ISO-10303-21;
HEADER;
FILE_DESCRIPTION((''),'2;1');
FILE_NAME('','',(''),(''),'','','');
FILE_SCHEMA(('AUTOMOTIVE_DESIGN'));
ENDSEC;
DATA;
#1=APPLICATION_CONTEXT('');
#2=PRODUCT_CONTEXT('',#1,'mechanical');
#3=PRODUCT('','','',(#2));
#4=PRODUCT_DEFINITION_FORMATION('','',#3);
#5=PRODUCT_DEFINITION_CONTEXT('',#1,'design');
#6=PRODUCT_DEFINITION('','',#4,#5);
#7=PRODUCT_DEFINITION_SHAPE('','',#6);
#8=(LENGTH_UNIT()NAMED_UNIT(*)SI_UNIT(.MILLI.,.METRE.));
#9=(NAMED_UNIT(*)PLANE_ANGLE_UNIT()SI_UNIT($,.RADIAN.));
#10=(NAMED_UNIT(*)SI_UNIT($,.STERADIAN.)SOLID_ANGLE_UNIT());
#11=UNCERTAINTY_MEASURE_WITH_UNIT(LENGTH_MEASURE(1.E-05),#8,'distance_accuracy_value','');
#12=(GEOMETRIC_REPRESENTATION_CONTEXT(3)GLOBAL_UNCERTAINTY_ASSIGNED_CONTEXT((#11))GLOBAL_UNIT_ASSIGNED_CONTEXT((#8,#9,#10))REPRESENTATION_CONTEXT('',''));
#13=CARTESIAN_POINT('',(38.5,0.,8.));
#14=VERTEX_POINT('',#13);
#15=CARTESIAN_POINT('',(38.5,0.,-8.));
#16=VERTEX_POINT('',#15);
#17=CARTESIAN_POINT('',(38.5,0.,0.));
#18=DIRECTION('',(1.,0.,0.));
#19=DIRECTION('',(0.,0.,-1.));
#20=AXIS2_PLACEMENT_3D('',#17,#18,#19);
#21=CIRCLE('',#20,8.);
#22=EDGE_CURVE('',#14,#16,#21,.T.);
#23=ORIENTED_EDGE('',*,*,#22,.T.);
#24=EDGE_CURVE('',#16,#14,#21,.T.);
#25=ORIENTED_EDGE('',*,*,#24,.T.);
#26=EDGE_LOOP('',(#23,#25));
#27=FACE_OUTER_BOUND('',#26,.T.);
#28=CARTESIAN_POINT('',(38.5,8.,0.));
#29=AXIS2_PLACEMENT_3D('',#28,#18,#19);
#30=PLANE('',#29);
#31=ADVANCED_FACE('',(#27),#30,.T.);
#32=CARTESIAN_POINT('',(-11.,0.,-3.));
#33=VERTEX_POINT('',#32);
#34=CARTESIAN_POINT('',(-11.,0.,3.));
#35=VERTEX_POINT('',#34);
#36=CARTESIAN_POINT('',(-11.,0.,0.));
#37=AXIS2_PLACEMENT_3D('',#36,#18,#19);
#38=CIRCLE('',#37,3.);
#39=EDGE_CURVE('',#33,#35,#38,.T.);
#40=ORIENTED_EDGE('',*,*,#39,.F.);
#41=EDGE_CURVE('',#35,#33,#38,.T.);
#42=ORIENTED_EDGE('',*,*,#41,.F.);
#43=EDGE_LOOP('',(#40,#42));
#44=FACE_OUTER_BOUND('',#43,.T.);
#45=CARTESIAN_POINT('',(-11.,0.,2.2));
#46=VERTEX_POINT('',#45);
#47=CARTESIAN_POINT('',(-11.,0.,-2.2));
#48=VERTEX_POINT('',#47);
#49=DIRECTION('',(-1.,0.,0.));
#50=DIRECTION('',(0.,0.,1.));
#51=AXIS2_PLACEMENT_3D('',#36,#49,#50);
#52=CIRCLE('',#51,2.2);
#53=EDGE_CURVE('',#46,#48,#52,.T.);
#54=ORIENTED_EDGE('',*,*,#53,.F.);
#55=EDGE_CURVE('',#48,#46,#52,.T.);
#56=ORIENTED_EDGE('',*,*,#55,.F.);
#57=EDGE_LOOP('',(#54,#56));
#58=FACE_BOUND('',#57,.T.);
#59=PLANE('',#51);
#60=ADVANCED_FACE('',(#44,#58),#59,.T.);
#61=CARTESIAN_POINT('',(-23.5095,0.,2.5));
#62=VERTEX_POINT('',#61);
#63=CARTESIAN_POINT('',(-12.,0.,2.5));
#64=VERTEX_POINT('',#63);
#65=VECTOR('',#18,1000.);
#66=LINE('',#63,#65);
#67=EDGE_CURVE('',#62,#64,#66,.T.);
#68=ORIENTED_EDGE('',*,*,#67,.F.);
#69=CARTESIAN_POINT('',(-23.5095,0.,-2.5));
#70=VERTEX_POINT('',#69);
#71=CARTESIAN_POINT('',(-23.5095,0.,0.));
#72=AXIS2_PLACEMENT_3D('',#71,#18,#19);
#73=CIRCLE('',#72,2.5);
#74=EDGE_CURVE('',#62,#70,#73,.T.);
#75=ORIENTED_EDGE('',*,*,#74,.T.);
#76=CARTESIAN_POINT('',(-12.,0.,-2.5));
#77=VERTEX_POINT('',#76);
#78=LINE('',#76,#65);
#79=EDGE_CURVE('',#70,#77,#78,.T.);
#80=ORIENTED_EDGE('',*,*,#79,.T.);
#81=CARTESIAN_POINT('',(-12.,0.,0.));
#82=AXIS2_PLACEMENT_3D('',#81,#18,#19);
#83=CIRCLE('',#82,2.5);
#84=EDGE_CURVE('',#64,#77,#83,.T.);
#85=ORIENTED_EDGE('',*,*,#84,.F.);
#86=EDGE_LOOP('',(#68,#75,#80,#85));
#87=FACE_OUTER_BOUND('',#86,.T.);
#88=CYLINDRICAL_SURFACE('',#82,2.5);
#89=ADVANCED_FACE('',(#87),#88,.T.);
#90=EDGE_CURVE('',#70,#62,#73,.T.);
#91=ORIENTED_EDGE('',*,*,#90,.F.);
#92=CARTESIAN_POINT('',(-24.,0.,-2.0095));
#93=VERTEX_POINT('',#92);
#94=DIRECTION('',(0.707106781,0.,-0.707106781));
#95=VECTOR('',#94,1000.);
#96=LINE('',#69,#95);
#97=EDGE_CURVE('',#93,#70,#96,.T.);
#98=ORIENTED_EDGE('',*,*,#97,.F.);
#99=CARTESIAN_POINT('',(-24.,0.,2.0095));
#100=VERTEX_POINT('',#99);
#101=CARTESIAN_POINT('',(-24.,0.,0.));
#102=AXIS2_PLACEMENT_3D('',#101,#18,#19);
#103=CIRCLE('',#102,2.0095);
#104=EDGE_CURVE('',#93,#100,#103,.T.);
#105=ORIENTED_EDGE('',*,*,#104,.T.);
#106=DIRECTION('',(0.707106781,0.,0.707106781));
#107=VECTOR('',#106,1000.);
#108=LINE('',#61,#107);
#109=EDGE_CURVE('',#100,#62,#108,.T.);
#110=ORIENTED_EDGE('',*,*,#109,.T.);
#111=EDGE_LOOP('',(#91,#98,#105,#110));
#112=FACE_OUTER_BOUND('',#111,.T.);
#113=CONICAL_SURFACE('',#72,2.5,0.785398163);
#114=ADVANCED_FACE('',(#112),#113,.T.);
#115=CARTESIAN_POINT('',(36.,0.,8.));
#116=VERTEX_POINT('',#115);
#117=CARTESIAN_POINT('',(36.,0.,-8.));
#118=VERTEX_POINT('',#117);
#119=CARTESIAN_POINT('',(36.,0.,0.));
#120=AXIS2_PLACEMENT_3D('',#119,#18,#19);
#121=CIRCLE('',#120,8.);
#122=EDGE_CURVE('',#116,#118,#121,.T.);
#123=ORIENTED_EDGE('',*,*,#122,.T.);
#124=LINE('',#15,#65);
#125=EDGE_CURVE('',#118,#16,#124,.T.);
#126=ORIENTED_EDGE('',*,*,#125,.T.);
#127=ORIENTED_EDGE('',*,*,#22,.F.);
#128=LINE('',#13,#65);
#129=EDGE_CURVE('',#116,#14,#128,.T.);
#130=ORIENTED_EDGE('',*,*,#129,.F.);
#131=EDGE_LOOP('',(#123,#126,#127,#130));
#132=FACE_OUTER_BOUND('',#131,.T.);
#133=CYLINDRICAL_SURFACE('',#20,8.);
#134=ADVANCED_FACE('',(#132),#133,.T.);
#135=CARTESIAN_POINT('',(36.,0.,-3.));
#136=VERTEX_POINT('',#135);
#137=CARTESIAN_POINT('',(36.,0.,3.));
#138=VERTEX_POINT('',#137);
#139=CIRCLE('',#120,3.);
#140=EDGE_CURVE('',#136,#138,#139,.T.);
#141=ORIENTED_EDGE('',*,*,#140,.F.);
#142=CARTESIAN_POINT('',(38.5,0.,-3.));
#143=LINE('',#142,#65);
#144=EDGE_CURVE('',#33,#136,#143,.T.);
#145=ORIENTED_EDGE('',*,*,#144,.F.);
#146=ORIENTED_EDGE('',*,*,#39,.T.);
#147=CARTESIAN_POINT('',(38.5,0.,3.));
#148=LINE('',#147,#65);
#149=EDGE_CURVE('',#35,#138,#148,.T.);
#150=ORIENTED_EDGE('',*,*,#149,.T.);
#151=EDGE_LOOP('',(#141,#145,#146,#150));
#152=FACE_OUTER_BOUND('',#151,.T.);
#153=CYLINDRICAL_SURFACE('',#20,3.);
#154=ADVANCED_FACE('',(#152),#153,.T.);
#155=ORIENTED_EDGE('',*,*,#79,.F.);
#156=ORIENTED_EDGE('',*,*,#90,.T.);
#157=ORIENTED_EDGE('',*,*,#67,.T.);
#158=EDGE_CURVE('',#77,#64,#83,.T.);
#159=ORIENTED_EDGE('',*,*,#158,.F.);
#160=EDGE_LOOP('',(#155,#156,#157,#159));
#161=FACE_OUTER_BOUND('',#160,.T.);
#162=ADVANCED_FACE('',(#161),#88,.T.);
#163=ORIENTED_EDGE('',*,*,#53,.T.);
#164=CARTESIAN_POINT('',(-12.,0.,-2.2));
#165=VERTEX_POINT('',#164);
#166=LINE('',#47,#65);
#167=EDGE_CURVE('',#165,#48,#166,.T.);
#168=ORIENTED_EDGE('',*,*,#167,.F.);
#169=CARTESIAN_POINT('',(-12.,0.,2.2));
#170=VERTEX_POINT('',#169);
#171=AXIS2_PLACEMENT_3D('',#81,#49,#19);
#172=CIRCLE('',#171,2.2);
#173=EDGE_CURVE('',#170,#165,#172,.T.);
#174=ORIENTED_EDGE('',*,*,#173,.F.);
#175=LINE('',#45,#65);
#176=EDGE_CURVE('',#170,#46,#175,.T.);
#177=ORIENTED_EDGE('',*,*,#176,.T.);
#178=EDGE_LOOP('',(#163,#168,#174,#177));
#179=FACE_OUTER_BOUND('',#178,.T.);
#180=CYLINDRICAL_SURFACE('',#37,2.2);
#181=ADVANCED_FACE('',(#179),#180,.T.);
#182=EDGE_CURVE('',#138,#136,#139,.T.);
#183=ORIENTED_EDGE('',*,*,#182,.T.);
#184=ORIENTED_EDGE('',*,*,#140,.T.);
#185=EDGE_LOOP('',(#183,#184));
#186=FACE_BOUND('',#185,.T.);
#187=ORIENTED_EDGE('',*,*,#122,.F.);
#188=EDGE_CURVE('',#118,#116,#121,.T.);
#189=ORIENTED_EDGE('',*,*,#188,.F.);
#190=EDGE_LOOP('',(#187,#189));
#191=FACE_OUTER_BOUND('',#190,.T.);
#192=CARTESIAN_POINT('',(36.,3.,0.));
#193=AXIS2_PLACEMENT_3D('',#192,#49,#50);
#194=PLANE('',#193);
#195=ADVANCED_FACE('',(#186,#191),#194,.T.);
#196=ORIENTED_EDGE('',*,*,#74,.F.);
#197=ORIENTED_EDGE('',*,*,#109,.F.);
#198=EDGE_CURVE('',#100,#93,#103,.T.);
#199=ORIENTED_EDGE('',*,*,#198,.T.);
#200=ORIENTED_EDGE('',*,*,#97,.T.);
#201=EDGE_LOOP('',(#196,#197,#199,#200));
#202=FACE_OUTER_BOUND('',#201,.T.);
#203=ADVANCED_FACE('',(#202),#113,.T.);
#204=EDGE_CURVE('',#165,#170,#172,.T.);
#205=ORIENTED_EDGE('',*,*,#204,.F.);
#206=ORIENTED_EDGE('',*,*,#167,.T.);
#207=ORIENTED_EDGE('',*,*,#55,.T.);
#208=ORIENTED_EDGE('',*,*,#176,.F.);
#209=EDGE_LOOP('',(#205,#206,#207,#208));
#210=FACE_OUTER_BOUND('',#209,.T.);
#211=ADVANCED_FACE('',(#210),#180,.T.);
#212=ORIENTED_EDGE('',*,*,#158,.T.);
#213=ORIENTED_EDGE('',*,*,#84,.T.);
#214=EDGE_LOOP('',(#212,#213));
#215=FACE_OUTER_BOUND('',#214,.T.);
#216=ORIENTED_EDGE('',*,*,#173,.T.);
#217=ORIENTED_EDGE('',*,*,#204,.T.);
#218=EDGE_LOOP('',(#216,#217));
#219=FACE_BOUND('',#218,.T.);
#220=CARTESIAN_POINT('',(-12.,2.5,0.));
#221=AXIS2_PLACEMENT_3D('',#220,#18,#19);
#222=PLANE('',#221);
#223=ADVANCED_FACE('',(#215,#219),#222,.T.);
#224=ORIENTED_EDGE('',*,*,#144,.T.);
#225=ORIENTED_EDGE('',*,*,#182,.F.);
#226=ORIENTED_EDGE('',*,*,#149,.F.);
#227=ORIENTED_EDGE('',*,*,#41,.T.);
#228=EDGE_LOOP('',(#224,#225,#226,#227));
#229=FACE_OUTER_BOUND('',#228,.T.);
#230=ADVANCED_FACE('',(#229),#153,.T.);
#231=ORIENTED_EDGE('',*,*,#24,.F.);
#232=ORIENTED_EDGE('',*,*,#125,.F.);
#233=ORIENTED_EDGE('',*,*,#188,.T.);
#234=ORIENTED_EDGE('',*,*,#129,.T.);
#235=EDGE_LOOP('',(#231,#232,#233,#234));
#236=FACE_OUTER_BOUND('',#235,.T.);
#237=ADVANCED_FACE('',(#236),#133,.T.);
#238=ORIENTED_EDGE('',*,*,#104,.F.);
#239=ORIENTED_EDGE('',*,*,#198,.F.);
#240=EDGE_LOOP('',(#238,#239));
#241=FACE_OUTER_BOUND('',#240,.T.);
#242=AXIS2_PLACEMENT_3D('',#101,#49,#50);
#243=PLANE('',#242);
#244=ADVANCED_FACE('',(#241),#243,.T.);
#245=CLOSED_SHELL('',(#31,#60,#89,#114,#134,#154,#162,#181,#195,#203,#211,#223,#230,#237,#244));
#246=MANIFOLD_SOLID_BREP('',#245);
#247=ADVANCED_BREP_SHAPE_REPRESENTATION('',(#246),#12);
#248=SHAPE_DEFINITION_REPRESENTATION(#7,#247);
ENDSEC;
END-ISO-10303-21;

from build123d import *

# Parameters (mm, degrees)
SKETCH2_W = 1
SKETCH2_H = 2.2


with BuildPart() as part:
    # Sketch1 → Revolve1 (revolve)
    with BuildSketch(Plane.XY, mode=Mode.PRIVATE) as revolve1_sk:
        Polygon((-11, 0), (-11, 3), (36, 3), (36, 8), (38.5, 8), (38.5, 0), align=None)
    revolve(revolve1_sk.sketch.rotate(Axis((38.5, 0, 0), (-1, 0, 0)), 90), axis=Axis((38.5, 0, 0), (-1, 0, 0)))

    # Sketch2 → Revolve2 (revolve)
    with BuildSketch(Plane.XY, mode=Mode.PRIVATE) as revolve2_sk:
        with Locations((-11.5, 1.1)):
            Rectangle(SKETCH2_W, SKETCH2_H)
    revolve(revolve2_sk.sketch.rotate(Axis((-11, 0, 0), (-1, 0, 0)), 90), axis=Axis((-11, 0, 0), (-1, 0, 0)))

    # Sketch3 → Revolve3 (revolve)
    with BuildSketch(Plane.XY, mode=Mode.PRIVATE) as revolve3_sk:
        Polygon((-24, 0), (-24, 2.0095), (-23.5095, 2.5), (-12, 2.5), (-12, 0), align=None)
    revolve(revolve3_sk.sketch.rotate(Axis((-12, 0, 0), (-1, 0, 0)), 90), axis=Axis((-12, 0, 0), (-1, 0, 0)))


solid = part.part
